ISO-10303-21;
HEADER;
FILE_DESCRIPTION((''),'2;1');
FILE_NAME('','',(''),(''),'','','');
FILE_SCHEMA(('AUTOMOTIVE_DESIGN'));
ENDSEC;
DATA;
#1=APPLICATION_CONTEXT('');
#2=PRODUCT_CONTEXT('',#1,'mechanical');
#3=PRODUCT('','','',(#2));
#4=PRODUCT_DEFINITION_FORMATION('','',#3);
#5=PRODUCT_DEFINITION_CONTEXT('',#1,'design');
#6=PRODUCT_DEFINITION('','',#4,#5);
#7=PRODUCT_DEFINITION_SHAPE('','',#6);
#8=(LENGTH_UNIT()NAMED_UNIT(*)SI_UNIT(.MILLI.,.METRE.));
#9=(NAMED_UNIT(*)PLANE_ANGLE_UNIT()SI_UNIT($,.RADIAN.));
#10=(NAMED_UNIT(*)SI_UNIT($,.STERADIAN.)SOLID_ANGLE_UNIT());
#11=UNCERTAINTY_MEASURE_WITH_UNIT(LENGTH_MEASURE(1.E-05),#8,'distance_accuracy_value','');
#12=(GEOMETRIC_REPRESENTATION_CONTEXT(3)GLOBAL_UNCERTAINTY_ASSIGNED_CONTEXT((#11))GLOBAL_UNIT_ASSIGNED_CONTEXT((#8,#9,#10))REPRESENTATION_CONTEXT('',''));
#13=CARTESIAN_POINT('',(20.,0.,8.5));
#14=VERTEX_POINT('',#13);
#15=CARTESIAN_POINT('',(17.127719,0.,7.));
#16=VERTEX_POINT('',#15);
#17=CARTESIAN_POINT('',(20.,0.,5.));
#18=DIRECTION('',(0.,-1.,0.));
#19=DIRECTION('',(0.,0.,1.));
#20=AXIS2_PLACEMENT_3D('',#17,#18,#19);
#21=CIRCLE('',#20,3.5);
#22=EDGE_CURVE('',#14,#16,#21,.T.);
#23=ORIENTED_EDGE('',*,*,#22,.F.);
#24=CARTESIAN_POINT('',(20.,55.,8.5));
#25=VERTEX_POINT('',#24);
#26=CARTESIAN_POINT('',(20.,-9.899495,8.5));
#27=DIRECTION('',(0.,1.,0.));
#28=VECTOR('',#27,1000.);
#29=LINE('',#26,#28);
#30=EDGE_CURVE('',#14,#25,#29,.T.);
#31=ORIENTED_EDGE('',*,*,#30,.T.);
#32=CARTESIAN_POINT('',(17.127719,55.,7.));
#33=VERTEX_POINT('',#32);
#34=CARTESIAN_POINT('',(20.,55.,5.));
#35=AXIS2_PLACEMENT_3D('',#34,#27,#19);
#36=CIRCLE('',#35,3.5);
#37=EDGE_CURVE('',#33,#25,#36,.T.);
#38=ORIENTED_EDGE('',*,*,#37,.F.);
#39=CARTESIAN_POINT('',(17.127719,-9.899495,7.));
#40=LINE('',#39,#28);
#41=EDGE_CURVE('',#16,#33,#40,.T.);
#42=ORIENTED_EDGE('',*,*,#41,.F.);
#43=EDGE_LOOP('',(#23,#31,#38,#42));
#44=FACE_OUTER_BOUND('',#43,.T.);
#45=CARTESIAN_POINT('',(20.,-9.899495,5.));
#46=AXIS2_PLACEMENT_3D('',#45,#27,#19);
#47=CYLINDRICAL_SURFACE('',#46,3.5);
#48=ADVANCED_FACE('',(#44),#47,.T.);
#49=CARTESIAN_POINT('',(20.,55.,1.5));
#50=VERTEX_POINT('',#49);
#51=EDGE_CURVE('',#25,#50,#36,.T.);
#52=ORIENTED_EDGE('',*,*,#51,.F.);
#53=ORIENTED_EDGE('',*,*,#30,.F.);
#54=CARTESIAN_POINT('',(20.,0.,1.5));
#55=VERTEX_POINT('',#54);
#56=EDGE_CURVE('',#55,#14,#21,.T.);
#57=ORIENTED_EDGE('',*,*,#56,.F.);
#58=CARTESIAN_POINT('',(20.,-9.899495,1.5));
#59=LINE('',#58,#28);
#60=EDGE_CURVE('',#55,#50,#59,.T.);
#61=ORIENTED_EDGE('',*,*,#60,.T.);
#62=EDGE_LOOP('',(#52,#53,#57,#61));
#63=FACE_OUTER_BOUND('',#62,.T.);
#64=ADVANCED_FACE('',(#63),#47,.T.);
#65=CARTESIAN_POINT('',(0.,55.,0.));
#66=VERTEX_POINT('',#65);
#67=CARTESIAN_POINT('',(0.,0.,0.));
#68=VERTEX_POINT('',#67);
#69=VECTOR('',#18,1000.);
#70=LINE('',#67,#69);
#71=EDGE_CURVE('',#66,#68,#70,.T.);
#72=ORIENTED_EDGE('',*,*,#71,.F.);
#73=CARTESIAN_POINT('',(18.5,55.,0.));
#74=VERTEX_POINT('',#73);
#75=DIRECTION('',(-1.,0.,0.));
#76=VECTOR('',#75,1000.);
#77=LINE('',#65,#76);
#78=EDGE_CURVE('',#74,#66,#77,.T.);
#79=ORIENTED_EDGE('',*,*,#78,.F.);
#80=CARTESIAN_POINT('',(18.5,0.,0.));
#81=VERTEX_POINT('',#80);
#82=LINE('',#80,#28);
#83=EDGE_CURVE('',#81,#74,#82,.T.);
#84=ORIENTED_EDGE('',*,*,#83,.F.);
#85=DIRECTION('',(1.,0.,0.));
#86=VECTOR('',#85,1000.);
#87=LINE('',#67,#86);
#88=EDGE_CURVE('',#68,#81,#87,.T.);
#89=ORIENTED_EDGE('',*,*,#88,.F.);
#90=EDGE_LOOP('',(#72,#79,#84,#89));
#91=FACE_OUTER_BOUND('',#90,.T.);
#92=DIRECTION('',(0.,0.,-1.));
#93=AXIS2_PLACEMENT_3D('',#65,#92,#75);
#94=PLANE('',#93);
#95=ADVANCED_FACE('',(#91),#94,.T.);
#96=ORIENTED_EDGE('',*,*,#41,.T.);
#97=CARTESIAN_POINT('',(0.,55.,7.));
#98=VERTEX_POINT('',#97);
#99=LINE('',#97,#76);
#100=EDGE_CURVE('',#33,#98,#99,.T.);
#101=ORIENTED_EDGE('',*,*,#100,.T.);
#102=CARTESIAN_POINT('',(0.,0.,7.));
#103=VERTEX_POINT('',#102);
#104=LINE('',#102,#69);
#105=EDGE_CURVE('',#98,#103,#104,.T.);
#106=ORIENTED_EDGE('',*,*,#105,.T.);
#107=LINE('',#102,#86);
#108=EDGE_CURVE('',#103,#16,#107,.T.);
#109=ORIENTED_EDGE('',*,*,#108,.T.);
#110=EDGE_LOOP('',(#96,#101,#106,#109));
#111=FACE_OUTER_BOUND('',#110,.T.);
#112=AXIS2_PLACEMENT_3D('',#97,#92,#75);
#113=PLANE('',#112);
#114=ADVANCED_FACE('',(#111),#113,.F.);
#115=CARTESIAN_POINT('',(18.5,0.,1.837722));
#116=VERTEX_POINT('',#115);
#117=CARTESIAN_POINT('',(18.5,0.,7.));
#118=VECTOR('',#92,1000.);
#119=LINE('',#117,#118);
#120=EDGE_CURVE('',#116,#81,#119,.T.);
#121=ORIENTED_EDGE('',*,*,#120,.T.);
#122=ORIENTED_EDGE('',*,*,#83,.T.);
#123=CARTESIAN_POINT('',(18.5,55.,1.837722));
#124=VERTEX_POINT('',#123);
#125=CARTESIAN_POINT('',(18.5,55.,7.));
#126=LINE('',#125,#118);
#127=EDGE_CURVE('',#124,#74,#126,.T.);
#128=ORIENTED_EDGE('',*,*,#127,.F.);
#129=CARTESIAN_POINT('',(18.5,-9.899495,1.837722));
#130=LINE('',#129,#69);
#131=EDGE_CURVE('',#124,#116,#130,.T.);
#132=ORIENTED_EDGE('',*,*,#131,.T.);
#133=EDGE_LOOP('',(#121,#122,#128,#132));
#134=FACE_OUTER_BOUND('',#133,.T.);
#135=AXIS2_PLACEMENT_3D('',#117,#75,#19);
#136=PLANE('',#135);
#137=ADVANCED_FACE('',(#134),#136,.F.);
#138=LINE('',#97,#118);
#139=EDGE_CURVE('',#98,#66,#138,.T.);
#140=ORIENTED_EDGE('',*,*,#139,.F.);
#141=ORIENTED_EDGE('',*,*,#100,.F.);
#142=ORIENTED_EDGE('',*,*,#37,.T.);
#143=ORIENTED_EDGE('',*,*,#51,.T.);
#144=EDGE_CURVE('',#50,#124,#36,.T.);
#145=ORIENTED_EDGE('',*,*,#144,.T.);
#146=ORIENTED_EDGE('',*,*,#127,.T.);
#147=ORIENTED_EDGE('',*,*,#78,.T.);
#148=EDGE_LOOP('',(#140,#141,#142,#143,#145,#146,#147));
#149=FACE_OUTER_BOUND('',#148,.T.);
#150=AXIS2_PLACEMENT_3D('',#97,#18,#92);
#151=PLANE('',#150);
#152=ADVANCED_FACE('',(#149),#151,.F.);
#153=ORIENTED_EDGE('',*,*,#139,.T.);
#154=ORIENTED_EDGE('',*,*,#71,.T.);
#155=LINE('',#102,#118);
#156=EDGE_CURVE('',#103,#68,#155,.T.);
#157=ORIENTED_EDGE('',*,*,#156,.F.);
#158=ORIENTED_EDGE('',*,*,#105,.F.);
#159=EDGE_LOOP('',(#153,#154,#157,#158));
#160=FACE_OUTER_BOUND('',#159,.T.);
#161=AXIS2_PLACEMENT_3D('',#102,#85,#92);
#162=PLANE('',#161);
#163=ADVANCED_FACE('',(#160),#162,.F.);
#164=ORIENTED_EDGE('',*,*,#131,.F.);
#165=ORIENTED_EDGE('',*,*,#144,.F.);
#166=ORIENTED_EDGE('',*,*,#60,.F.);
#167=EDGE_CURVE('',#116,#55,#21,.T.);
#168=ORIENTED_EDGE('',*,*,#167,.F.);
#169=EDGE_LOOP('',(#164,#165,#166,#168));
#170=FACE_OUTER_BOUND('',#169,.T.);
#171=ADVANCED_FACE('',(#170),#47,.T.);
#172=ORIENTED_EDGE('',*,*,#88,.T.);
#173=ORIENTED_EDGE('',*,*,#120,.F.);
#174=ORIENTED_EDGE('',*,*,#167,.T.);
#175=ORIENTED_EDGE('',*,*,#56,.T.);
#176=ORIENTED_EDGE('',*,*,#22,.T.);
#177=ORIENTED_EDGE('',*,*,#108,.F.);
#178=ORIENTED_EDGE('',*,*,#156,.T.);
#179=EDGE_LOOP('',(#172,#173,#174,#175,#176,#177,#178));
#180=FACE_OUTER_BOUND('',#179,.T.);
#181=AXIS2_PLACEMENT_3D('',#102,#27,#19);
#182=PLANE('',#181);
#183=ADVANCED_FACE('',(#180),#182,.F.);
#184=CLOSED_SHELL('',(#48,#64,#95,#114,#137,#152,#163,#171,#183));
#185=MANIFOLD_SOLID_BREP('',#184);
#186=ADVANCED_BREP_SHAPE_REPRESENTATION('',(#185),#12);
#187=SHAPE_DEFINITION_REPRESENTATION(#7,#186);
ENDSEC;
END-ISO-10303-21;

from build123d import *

# Parameters (mm, degrees)
SKETCH_1_W      = 18.5
SKETCH_1_H      = 55
EXTRUDE_1_DEPTH = 7
SKETCH_2_R      = 3.5
EXTRUDE_2_DEPTH = 55


with BuildPart() as part:
    # 草图1 → 凸台-拉伸1 (new body)
    with BuildSketch(Plane.XY):
        with Locations((9.25, 27.5)):
            Rectangle(SKETCH_1_W, SKETCH_1_H)
    extrude(amount=EXTRUDE_1_DEPTH)

    # 草图2 → 凸台-拉伸2 (add)
    with BuildSketch(Plane(origin=(0, 55, 0), x_dir=(1, 0, 0), z_dir=(0, 1, 0))):
        with Locations((20, -5)):
            Circle(SKETCH_2_R)
    extrude(amount=-EXTRUDE_2_DEPTH)


solid = part.part
